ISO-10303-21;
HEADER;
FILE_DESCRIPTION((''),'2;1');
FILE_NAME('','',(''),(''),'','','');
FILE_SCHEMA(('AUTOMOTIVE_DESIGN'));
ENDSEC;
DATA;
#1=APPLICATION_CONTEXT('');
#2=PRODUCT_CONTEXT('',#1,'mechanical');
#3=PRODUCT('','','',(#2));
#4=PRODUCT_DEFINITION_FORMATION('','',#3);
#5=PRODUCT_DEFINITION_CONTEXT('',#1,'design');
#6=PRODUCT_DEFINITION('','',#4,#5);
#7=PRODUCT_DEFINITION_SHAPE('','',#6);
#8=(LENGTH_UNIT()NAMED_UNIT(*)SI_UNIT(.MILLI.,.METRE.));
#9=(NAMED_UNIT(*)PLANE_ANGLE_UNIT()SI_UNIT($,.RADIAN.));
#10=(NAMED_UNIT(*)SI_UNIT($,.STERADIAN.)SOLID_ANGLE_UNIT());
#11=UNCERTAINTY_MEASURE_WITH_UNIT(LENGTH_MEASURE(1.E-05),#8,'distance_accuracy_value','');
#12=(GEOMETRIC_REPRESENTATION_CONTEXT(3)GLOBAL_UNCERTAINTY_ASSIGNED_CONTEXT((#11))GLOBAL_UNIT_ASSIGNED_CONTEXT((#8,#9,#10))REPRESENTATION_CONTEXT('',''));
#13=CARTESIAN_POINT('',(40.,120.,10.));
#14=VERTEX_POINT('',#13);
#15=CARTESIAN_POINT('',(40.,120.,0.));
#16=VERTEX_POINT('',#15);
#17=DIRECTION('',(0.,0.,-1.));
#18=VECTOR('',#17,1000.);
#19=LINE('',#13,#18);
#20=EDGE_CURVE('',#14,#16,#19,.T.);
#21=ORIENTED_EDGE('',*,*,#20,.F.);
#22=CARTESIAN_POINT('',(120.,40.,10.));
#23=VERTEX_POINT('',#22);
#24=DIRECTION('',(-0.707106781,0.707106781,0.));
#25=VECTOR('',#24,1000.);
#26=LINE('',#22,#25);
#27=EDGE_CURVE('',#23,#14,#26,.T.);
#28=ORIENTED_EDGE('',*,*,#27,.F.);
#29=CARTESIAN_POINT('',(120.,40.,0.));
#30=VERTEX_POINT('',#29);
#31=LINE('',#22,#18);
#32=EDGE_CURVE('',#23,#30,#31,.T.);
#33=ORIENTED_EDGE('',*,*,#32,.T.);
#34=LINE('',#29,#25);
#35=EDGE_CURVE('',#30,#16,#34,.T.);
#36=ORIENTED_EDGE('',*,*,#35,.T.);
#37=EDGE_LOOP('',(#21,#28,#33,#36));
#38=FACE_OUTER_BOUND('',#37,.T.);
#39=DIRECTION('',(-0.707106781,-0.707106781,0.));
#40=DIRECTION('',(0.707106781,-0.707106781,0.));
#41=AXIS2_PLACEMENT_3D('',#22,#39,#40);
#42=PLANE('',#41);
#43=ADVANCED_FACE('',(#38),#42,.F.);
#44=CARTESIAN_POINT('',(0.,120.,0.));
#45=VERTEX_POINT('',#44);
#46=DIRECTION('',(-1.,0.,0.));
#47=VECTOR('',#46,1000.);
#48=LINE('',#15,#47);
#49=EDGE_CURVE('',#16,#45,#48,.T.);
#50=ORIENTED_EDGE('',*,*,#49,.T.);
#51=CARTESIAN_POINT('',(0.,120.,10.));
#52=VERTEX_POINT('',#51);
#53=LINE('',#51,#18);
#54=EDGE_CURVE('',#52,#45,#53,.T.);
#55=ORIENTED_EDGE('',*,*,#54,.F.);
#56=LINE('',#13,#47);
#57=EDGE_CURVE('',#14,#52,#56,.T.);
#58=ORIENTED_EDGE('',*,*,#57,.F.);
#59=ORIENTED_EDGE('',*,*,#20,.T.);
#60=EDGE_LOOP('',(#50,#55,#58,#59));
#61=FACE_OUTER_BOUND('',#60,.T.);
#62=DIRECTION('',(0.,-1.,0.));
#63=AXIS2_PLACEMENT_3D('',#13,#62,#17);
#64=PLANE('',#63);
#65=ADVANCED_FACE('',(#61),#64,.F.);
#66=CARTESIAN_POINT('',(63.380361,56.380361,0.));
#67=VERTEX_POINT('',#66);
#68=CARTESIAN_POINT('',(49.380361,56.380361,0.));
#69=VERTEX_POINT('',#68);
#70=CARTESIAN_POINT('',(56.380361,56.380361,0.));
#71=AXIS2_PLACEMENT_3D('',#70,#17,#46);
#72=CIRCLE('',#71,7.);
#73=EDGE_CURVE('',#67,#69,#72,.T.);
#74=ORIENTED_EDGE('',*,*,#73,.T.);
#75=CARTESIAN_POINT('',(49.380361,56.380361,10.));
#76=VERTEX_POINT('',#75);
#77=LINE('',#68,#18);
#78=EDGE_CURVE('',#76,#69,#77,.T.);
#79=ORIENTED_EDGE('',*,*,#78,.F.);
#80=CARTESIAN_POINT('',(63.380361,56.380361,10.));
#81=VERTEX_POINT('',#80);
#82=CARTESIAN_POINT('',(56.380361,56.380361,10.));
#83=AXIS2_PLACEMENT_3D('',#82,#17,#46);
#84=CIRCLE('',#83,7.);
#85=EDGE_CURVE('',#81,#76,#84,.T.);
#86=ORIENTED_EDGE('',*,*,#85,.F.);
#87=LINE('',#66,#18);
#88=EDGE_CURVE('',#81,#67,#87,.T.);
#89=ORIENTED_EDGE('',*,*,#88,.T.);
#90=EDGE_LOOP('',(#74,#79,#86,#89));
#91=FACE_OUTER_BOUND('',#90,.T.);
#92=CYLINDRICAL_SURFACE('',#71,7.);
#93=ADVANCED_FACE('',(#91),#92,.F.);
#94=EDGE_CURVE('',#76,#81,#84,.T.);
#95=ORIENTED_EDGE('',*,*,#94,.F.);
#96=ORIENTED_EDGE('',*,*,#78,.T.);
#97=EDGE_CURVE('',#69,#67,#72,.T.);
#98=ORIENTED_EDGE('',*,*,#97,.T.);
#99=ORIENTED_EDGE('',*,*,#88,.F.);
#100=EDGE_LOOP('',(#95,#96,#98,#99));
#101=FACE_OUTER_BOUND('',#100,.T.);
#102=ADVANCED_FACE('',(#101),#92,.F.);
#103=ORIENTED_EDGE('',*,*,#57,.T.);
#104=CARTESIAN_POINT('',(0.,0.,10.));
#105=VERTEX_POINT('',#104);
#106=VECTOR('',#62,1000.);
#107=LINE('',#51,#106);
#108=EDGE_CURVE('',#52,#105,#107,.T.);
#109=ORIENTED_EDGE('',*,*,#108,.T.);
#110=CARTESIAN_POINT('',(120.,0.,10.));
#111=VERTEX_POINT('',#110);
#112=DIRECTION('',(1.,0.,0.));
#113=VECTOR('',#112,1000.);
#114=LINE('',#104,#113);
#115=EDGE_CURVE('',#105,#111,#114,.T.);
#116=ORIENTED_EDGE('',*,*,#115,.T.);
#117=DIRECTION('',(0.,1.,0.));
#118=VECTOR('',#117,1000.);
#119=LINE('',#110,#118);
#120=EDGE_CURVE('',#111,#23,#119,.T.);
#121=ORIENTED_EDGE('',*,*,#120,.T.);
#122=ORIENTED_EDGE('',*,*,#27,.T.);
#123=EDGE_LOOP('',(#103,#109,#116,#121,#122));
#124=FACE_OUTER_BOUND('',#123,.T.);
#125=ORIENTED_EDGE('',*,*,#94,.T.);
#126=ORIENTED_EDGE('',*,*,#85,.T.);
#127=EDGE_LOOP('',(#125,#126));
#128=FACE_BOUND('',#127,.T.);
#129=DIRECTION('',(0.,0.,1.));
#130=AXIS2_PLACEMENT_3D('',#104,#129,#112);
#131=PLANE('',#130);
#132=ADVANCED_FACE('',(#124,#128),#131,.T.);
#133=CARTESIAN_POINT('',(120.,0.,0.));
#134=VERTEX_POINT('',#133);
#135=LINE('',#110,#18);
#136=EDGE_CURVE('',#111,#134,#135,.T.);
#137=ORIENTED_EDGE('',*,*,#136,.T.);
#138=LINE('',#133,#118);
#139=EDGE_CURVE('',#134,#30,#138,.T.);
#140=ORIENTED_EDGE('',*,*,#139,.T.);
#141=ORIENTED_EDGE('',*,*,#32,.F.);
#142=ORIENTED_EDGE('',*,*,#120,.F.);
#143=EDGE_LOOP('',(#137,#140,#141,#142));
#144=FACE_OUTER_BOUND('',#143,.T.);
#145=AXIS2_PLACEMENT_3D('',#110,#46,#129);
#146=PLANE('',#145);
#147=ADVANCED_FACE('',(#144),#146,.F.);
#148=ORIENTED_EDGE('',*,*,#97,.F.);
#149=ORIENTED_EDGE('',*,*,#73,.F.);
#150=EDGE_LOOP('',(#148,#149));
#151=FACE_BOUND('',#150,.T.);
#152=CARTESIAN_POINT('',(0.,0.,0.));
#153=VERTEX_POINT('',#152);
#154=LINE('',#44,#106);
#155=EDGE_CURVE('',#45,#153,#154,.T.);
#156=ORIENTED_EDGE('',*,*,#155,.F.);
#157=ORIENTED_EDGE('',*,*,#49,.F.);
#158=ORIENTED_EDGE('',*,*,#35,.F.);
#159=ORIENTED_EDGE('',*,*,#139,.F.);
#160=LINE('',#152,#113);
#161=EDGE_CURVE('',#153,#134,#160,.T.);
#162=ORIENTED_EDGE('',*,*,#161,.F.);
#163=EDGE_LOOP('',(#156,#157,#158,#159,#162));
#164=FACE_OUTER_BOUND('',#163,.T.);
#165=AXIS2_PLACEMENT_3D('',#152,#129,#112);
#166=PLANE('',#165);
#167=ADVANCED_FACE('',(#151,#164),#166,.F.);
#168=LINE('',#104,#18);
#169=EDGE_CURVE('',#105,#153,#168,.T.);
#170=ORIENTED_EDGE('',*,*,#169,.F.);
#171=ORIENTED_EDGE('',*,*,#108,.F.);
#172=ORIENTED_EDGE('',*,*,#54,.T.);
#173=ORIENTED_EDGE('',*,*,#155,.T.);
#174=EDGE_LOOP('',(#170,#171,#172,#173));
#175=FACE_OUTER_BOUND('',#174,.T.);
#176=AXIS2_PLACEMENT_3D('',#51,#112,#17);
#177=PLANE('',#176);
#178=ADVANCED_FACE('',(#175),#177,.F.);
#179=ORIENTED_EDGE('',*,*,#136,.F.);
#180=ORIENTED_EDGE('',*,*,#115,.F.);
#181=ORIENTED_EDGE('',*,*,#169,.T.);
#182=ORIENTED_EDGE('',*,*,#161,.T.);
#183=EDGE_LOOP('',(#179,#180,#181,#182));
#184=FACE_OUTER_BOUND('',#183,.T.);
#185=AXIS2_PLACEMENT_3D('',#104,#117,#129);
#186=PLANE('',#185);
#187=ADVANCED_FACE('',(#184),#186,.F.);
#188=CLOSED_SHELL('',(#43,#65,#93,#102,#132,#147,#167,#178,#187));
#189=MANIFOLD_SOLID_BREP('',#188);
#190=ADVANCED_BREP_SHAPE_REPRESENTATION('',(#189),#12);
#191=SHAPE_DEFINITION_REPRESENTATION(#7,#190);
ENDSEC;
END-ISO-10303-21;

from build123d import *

# Parameters (mm, degrees)
EXTRUDE_1_DEPTH     = 10
HOLE_WIZARD_M16_1_D = 14


with BuildPart() as part:
    # 草图1 → 凸台-拉伸1 (new body)
    with BuildSketch(Plane.XY):
        Polygon((0, 120), (0, 0), (120, 0), (120, 40), (40, 120), align=None)
    extrude(amount=EXTRUDE_1_DEPTH)

    # M16 螺纹孔1 (through all)
    with Locations(Plane(origin=(0, 0, 0), x_dir=(-1, 0, 0), z_dir=(0, 0, -1))):
        with Locations((-56.380361078, 56.380361078)):
            Hole(HOLE_WIZARD_M16_1_D / 2)


solid = part.part
